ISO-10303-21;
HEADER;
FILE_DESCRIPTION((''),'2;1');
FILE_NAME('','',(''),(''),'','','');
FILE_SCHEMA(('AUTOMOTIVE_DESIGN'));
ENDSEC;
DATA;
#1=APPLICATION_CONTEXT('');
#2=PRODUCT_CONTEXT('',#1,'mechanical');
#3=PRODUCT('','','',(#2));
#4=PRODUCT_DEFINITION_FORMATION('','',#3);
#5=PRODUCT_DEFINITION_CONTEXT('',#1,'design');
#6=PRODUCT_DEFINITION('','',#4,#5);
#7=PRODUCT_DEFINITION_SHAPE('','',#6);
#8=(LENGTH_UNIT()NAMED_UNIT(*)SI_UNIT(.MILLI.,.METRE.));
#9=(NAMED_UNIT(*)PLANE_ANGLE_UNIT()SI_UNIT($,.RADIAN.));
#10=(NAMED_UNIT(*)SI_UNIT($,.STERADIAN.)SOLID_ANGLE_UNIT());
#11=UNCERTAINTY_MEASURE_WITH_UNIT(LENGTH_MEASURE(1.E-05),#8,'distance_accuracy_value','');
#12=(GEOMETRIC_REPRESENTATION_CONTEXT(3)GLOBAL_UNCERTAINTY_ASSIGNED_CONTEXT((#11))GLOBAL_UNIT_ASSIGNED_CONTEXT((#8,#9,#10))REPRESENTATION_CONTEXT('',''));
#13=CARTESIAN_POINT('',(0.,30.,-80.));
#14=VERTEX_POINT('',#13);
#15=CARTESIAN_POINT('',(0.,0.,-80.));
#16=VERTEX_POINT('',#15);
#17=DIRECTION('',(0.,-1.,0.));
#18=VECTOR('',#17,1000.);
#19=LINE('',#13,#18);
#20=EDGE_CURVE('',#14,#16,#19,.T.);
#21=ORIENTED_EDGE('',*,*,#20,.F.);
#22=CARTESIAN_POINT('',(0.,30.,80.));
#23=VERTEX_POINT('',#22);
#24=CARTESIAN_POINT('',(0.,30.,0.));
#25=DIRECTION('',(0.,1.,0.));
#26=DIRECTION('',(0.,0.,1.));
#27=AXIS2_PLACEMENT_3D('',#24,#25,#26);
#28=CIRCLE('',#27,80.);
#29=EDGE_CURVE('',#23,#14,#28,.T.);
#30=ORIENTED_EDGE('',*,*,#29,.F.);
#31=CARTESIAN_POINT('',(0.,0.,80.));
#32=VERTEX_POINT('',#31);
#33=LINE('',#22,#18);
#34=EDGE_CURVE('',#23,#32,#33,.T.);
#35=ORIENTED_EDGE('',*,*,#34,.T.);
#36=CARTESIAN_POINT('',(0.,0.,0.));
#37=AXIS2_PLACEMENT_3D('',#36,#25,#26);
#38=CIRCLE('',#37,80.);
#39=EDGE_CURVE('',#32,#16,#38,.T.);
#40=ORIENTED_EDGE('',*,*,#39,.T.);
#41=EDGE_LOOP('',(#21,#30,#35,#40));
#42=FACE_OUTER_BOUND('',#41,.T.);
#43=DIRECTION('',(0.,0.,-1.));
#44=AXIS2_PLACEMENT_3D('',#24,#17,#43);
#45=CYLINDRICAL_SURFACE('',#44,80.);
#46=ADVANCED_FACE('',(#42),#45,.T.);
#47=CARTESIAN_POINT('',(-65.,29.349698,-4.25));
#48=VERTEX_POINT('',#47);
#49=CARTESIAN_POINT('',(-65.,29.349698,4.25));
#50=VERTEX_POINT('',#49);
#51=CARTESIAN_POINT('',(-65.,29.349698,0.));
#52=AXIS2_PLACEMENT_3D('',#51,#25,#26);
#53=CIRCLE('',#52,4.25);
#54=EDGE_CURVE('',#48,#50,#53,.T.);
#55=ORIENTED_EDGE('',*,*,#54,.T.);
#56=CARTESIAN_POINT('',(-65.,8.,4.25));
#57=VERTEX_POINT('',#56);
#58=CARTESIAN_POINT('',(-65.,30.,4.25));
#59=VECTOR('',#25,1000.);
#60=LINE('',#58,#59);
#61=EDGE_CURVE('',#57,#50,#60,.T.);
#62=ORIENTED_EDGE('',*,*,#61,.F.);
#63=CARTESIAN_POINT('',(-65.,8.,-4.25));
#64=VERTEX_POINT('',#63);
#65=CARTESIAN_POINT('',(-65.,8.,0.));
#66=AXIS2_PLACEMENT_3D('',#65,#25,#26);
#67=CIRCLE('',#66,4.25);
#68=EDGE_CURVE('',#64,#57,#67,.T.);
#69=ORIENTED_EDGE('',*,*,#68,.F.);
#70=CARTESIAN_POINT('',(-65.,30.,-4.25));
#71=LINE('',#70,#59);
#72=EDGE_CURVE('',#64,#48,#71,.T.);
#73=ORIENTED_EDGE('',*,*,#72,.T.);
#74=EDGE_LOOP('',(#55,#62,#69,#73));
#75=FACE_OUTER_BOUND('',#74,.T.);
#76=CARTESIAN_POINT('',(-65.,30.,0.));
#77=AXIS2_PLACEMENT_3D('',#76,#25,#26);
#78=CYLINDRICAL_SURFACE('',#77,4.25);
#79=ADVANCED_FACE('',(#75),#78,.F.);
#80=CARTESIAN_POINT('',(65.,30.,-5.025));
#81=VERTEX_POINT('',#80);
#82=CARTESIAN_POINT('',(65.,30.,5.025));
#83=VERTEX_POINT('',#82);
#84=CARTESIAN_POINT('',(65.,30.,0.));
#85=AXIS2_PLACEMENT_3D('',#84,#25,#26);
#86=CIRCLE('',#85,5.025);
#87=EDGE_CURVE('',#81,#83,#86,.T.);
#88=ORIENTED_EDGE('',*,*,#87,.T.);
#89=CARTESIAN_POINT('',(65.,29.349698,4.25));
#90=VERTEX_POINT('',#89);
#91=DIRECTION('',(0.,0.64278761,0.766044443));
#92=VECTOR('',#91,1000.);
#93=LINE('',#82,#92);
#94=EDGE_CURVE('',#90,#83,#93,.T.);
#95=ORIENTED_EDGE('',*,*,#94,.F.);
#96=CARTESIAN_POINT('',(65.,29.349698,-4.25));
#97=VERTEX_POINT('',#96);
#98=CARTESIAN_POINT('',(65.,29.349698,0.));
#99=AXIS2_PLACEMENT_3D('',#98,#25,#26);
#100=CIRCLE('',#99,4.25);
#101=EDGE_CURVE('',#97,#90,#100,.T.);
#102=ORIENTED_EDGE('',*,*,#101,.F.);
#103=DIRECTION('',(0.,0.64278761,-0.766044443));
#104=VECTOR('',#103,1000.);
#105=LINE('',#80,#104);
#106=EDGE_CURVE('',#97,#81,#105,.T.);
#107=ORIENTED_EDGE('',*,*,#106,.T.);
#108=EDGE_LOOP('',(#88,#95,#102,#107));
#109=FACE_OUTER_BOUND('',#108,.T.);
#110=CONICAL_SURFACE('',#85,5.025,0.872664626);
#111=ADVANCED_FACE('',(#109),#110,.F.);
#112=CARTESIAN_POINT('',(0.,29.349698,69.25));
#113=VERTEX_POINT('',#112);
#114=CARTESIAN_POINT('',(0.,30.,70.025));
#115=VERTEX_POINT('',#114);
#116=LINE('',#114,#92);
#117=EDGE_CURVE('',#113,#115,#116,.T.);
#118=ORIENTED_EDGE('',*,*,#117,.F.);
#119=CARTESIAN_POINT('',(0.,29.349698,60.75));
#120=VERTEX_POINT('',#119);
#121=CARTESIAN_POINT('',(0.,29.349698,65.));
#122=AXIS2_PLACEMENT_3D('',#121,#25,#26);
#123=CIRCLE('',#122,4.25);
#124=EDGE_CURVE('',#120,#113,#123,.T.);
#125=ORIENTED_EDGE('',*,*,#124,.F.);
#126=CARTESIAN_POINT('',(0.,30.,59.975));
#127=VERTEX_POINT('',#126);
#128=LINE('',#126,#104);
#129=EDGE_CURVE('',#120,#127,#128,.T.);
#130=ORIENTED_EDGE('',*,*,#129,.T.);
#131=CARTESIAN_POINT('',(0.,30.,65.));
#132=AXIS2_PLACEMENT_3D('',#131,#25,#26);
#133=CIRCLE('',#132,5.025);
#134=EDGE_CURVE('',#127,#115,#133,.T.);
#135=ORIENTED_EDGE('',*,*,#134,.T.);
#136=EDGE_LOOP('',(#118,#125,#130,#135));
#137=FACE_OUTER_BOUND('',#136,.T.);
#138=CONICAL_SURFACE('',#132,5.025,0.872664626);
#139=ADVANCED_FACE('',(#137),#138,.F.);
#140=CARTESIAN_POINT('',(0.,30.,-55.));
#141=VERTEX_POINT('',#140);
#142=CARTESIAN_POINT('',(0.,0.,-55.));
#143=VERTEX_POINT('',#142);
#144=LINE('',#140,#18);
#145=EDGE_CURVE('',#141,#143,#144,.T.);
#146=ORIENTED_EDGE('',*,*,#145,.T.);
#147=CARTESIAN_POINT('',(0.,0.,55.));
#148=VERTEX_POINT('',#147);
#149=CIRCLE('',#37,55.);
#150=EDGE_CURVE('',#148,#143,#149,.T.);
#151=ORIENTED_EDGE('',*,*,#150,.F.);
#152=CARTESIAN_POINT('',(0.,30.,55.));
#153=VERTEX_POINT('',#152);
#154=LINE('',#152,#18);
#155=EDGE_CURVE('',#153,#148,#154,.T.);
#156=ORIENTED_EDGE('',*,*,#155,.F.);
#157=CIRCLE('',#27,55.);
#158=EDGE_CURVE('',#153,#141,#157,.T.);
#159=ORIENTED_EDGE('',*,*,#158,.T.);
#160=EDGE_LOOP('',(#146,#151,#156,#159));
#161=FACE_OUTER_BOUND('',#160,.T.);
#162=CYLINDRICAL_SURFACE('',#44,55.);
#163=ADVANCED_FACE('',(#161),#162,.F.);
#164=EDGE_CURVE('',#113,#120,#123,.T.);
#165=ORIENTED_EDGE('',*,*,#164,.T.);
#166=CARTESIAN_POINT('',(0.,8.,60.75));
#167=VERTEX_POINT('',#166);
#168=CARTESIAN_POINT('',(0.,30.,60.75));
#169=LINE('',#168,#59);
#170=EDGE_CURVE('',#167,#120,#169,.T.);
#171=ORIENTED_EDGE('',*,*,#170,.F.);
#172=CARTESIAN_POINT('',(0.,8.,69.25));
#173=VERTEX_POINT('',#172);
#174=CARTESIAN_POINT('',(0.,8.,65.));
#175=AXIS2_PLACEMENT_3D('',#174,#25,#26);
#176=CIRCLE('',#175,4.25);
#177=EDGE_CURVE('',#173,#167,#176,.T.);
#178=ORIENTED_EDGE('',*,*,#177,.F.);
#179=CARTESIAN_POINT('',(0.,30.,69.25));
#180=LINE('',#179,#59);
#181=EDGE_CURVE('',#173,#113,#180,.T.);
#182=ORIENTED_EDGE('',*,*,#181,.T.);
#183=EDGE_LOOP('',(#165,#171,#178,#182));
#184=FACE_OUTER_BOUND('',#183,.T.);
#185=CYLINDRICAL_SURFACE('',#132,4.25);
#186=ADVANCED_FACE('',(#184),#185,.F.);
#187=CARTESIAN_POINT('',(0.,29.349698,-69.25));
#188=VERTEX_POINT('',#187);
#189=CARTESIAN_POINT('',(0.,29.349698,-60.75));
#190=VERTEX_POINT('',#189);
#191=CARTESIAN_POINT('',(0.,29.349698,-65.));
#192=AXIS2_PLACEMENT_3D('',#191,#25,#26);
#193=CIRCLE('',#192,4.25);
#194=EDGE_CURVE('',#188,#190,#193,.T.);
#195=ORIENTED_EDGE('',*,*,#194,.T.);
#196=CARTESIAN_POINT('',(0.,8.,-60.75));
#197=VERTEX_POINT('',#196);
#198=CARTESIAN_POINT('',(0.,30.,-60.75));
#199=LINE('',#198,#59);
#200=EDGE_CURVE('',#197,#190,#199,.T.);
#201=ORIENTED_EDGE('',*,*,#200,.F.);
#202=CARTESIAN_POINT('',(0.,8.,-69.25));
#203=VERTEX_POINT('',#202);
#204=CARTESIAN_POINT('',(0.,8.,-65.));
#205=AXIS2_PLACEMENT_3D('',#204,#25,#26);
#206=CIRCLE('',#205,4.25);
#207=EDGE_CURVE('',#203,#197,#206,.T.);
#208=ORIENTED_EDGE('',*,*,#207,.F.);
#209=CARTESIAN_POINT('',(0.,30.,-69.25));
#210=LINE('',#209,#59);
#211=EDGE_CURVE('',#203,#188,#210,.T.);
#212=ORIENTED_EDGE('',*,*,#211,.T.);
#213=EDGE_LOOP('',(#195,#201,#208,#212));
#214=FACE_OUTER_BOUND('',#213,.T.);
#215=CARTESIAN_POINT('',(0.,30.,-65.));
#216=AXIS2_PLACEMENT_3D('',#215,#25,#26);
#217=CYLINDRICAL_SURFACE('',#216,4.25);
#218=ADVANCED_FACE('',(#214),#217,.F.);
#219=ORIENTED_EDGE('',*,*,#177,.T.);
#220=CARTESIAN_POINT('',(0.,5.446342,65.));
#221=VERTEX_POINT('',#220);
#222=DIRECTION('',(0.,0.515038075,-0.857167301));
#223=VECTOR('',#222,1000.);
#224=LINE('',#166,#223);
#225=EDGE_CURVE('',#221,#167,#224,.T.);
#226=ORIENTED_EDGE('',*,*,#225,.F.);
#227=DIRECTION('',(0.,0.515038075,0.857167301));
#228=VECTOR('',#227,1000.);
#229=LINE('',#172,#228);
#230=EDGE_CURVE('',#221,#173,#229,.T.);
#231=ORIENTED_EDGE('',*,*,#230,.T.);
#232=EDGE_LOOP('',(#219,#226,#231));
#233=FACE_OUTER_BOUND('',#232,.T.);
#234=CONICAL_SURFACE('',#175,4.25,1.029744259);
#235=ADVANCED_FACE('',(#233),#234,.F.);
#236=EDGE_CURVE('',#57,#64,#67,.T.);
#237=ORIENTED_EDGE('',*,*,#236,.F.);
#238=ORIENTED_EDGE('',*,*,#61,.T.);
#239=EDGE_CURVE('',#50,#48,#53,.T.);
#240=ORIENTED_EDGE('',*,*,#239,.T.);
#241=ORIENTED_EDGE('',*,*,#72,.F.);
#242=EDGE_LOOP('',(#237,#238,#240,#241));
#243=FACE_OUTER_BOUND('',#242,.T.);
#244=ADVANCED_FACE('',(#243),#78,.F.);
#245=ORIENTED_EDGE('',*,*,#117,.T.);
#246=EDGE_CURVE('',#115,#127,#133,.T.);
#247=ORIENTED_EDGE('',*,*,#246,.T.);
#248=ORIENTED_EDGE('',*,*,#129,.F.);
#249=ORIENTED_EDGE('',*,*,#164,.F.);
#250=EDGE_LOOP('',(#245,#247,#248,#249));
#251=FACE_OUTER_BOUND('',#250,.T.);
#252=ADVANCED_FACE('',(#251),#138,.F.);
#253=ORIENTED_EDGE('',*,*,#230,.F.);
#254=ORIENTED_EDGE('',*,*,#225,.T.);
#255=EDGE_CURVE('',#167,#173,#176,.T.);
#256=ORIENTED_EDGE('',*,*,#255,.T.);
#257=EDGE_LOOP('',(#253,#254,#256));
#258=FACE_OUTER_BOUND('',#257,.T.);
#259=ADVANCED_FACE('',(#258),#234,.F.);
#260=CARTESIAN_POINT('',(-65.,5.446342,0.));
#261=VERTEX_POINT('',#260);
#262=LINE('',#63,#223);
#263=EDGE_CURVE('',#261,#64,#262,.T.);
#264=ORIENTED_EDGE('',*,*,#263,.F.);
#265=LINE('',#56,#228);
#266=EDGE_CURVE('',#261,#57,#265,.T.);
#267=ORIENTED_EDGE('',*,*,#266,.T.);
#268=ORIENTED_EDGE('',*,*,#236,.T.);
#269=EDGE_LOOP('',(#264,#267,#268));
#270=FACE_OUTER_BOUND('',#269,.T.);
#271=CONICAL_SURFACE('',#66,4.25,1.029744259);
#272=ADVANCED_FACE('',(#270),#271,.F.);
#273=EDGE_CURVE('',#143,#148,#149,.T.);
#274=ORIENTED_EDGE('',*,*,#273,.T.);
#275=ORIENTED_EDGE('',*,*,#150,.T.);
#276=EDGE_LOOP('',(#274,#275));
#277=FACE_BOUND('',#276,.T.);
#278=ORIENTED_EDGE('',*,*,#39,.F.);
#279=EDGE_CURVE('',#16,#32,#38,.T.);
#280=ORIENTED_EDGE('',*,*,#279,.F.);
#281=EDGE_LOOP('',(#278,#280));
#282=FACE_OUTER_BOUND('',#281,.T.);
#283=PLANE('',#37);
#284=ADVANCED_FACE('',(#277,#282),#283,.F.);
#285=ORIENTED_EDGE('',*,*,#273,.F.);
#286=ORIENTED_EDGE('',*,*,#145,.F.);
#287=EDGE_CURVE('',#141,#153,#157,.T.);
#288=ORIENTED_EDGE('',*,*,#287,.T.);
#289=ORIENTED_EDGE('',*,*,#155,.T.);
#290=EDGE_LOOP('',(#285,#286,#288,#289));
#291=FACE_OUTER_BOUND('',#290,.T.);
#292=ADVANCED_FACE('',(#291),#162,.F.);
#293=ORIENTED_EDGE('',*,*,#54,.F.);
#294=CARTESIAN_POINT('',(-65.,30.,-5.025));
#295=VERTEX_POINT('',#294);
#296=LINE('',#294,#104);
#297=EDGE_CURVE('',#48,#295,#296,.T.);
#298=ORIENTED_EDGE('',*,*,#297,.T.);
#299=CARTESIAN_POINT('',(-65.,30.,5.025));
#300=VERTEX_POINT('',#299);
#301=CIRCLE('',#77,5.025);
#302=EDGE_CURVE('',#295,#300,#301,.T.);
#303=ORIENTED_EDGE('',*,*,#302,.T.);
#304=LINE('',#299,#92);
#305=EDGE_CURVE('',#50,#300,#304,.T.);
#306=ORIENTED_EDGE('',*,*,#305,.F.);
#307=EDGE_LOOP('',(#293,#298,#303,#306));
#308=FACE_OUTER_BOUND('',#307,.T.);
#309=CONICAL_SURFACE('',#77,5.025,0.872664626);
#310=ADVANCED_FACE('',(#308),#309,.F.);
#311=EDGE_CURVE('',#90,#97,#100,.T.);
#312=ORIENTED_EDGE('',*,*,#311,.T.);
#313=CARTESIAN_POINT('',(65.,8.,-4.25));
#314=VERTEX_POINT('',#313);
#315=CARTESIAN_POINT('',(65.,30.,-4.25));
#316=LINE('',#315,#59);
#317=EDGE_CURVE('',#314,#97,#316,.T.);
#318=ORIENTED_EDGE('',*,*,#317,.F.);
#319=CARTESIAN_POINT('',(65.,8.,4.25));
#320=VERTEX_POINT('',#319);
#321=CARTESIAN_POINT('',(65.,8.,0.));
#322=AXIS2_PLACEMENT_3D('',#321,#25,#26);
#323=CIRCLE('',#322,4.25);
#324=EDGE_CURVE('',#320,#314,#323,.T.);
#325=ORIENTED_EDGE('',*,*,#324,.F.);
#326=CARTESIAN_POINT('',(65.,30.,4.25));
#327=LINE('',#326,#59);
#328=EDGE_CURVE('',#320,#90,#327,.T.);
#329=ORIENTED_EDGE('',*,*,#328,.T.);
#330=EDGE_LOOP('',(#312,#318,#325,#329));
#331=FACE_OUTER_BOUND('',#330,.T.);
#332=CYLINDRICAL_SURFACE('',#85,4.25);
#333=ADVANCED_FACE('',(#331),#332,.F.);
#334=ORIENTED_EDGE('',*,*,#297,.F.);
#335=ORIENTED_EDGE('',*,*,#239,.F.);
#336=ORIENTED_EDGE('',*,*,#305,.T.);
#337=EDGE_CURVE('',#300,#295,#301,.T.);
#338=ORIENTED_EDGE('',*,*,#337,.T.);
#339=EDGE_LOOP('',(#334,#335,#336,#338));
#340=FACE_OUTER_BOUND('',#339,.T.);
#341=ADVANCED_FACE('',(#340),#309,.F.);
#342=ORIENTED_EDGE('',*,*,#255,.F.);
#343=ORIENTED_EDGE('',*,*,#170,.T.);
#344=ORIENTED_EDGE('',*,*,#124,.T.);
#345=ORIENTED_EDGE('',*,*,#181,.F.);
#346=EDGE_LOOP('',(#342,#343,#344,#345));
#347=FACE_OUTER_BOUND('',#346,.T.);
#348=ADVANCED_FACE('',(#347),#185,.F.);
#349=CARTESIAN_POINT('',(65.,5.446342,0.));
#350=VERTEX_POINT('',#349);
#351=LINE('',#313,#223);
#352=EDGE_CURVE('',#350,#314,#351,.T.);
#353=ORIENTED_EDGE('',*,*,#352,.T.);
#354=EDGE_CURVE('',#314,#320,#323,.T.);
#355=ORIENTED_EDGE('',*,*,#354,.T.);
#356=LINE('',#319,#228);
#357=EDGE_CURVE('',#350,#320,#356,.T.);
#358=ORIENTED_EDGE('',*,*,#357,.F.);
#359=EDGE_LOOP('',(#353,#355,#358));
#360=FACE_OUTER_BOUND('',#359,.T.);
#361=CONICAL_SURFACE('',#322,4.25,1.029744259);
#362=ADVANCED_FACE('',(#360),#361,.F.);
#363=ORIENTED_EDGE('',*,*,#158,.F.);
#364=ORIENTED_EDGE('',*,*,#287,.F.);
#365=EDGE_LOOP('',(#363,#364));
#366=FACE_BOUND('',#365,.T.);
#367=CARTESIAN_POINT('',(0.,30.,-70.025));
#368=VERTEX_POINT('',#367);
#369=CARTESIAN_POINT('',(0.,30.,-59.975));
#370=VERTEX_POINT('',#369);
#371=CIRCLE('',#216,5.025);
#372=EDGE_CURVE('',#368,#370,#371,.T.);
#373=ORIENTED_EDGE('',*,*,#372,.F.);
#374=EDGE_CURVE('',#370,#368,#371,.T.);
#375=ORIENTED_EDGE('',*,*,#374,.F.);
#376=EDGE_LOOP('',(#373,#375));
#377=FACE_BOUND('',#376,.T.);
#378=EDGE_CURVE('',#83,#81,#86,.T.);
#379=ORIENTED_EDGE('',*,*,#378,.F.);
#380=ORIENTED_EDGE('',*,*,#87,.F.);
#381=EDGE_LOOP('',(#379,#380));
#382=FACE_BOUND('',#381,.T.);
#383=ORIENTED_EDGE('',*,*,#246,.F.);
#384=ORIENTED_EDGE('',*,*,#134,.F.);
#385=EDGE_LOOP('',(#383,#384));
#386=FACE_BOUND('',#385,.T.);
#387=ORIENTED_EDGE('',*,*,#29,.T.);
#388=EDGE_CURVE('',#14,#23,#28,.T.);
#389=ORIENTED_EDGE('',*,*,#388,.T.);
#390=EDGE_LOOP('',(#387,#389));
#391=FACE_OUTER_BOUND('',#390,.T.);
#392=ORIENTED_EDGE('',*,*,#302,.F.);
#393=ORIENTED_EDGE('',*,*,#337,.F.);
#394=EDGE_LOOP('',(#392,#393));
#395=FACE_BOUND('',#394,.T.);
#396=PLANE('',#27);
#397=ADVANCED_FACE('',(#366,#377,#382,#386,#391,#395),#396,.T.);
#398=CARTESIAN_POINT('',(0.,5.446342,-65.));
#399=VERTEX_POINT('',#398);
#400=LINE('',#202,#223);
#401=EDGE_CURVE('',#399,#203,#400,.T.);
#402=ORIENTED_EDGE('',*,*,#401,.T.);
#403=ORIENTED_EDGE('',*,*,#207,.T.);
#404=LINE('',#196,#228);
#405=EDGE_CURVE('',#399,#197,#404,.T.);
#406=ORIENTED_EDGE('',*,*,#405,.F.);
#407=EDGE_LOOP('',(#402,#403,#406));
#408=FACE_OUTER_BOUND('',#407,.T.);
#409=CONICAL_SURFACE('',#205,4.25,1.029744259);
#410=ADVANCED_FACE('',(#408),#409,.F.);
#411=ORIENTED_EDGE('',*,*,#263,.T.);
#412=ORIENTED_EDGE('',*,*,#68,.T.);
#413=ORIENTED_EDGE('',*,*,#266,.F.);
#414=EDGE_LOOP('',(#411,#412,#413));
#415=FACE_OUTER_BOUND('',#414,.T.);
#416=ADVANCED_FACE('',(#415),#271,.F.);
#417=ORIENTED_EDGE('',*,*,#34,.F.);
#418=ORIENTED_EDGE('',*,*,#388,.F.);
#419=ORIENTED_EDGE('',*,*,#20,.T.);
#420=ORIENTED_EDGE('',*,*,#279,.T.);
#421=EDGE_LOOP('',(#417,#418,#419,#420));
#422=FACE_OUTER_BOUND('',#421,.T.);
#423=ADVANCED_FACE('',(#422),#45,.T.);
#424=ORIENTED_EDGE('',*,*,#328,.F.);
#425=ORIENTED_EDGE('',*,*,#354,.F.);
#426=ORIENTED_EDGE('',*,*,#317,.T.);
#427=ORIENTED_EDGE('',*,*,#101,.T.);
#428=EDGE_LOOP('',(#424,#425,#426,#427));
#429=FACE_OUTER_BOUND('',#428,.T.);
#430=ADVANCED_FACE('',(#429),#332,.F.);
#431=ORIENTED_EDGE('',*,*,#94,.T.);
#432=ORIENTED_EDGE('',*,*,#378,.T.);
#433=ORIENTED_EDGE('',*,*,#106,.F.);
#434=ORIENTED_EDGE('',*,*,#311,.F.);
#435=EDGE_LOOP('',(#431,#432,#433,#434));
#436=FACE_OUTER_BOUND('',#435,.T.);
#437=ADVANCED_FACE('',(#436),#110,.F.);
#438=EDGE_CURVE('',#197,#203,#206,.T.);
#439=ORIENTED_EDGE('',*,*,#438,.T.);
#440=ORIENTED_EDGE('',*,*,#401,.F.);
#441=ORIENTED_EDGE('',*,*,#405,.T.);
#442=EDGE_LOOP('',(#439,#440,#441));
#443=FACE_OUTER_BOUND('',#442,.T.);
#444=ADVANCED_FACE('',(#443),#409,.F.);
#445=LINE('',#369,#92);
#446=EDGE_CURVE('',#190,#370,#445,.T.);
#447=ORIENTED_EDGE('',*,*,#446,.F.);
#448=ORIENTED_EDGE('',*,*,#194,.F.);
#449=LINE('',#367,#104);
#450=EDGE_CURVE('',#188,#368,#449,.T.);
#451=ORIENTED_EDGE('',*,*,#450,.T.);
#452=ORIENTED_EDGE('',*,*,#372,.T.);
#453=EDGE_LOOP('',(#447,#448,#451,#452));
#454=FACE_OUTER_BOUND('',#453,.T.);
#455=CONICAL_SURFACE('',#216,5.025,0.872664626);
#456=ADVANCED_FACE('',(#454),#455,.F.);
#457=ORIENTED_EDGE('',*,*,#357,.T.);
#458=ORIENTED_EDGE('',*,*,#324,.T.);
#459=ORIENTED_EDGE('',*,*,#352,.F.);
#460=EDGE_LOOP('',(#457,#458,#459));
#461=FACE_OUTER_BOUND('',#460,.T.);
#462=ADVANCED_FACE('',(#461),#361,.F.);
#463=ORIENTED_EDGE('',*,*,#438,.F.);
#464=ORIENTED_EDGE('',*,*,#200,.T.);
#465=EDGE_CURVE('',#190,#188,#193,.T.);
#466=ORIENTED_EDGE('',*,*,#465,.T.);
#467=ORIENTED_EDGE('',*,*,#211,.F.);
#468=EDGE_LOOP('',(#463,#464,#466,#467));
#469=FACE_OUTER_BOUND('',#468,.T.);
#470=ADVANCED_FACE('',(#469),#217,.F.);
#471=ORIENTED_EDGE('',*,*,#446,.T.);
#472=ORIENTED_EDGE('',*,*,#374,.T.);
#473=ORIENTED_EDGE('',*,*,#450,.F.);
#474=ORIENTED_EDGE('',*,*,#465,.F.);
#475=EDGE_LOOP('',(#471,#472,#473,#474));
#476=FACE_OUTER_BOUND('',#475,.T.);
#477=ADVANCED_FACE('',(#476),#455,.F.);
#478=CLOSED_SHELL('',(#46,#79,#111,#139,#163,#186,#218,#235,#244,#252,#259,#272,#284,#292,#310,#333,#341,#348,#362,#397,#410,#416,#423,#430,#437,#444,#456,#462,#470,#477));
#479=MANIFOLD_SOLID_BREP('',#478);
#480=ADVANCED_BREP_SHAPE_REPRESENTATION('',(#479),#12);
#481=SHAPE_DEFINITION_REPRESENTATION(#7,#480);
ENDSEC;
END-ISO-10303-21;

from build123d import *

# Parameters (mm, degrees)
SKETCH1_R                    = 80
SKETCH1_R_2                  = 55
BOSS_EXTRUDE1_DEPTH          = 30
M10_TAPPED_HOLE1_D           = 8.5
M10_TAPPED_HOLE1_DEPTH       = 22
M10_TAPPED_HOLE1_CSINK_D     = 10.05
M10_TAPPED_HOLE1_CSINK_ANGLE = 100
M10_TAPPED_HOLE1_TIP         = 2.553657631


with BuildPart() as part:
    # Sketch1 → Boss-Extrude1 (new body)
    with BuildSketch(Plane(origin=(0, 0, 0), x_dir=(1, 0, 0), z_dir=(0, 1, 0))):
        with Locations(Location((0, 0, 0), (0, 0, 270))):
            Circle(SKETCH1_R)
        with Locations(Location((0, 0, 0), (0, 0, 270))):
            Circle(SKETCH1_R_2, mode=Mode.SUBTRACT)
    extrude(amount=BOSS_EXTRUDE1_DEPTH)

    # M10 Tapped Hole1
    with Locations(Plane(origin=(0, 30, 0), x_dir=(1, 0, 0), z_dir=(0, 1, 0))):
        with Locations((0, 65), (65, 0), (0, -65), (-65, 0)):
            CounterSinkHole(M10_TAPPED_HOLE1_D / 2, M10_TAPPED_HOLE1_CSINK_D / 2, depth=M10_TAPPED_HOLE1_DEPTH, counter_sink_angle=M10_TAPPED_HOLE1_CSINK_ANGLE)
            with Locations((0, 0, -(M10_TAPPED_HOLE1_DEPTH + M10_TAPPED_HOLE1_TIP / 2))):  # 118° drill point
                Cone(0, M10_TAPPED_HOLE1_D / 2, M10_TAPPED_HOLE1_TIP, mode=Mode.SUBTRACT)


solid = part.part
